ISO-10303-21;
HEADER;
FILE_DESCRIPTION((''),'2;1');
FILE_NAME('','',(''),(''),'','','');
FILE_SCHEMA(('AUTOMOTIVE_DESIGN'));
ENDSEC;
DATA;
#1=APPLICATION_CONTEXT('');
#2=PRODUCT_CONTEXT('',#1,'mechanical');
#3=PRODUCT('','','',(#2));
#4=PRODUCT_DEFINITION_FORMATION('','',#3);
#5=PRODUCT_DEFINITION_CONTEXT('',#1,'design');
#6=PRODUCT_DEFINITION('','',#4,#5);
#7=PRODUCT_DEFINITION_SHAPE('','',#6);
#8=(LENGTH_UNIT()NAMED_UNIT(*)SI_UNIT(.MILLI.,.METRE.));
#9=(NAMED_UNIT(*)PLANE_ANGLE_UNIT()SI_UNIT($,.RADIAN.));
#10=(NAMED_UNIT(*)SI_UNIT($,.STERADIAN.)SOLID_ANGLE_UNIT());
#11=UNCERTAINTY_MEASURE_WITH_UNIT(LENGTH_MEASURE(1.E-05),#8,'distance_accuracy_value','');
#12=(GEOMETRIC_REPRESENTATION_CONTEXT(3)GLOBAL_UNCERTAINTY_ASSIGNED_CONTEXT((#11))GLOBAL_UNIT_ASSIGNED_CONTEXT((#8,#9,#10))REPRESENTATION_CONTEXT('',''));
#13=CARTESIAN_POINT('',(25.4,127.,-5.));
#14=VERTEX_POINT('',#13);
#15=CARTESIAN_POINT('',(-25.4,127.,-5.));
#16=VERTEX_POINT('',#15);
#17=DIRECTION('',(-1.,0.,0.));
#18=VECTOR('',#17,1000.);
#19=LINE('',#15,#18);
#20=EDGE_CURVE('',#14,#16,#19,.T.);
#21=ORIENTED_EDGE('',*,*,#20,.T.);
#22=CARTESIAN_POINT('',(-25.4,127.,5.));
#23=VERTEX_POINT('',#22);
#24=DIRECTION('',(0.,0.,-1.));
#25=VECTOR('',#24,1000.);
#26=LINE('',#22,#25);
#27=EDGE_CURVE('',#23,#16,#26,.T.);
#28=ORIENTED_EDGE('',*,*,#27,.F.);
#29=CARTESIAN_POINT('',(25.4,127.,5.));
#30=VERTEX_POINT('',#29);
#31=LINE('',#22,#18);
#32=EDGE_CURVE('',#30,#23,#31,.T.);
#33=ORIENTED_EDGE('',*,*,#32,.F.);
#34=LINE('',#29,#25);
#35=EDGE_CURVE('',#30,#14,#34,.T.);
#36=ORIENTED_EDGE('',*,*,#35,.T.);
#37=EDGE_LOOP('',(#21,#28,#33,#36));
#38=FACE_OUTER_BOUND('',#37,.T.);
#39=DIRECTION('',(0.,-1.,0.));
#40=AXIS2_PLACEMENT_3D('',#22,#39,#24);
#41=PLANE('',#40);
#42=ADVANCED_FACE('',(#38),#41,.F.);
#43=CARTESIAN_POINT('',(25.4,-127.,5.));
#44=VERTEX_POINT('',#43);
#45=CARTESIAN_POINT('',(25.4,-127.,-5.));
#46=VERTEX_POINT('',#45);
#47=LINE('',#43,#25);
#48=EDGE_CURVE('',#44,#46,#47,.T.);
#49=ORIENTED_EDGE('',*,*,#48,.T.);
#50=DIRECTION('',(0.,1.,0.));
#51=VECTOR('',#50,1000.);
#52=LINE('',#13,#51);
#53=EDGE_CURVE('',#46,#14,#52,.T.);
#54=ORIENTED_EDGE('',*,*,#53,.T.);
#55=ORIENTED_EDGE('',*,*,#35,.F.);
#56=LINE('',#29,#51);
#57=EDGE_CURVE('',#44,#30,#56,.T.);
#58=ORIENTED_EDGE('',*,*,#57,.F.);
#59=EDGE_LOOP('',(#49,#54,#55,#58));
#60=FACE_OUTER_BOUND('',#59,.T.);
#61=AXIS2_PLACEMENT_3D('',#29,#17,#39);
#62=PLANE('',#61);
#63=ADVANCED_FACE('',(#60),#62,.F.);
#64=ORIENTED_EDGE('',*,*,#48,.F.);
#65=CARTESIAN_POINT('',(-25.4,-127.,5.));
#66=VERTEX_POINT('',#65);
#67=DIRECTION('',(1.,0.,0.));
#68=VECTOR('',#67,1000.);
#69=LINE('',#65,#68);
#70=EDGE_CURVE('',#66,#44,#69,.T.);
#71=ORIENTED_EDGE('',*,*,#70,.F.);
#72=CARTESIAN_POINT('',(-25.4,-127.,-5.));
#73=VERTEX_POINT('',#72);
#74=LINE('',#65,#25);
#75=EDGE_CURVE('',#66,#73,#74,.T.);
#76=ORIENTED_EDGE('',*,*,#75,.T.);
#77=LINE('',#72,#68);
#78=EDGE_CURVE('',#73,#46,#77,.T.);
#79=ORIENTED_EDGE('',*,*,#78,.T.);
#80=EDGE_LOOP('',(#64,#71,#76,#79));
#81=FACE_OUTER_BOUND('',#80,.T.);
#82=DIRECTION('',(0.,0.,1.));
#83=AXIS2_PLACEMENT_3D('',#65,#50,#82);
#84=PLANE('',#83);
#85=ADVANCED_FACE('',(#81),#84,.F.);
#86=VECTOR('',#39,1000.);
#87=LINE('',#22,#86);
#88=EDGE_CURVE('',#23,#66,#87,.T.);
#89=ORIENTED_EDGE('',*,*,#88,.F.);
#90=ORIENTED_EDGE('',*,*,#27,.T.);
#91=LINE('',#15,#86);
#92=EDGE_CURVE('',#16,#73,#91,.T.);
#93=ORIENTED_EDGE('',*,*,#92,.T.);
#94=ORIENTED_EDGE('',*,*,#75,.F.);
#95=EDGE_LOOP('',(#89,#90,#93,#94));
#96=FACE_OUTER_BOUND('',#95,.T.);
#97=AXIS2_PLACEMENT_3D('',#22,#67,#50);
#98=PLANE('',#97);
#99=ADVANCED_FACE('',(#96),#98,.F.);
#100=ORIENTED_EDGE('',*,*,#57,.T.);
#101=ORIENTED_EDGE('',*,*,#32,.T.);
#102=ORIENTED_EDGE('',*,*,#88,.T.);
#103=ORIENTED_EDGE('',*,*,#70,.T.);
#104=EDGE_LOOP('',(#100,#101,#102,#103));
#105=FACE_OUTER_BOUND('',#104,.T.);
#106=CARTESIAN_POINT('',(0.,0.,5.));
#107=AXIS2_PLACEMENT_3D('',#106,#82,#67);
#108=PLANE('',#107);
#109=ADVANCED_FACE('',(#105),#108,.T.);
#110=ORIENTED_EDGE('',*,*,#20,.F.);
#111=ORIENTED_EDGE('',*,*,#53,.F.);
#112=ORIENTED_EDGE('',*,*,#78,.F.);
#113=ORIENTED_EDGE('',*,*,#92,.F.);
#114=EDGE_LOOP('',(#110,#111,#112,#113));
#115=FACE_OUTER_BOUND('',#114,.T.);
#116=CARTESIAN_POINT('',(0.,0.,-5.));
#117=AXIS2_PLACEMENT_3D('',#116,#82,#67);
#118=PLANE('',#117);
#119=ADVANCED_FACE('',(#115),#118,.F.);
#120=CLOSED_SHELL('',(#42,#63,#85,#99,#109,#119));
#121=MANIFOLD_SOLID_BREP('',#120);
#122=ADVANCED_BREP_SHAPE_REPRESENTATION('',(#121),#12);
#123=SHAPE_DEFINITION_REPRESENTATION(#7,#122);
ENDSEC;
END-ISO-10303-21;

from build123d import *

# Parameters (mm, degrees)
SKETCH1_W           = 50.8
SKETCH1_H           = 254
BOSS_EXTRUDE1_DEPTH = 5


with BuildPart() as part:
    # Sketch1 → Boss-Extrude1 (new, symmetric)
    with BuildSketch(Plane.XY):
        Rectangle(SKETCH1_W, SKETCH1_H)
    extrude(amount=BOSS_EXTRUDE1_DEPTH, both=True)


solid = part.part
